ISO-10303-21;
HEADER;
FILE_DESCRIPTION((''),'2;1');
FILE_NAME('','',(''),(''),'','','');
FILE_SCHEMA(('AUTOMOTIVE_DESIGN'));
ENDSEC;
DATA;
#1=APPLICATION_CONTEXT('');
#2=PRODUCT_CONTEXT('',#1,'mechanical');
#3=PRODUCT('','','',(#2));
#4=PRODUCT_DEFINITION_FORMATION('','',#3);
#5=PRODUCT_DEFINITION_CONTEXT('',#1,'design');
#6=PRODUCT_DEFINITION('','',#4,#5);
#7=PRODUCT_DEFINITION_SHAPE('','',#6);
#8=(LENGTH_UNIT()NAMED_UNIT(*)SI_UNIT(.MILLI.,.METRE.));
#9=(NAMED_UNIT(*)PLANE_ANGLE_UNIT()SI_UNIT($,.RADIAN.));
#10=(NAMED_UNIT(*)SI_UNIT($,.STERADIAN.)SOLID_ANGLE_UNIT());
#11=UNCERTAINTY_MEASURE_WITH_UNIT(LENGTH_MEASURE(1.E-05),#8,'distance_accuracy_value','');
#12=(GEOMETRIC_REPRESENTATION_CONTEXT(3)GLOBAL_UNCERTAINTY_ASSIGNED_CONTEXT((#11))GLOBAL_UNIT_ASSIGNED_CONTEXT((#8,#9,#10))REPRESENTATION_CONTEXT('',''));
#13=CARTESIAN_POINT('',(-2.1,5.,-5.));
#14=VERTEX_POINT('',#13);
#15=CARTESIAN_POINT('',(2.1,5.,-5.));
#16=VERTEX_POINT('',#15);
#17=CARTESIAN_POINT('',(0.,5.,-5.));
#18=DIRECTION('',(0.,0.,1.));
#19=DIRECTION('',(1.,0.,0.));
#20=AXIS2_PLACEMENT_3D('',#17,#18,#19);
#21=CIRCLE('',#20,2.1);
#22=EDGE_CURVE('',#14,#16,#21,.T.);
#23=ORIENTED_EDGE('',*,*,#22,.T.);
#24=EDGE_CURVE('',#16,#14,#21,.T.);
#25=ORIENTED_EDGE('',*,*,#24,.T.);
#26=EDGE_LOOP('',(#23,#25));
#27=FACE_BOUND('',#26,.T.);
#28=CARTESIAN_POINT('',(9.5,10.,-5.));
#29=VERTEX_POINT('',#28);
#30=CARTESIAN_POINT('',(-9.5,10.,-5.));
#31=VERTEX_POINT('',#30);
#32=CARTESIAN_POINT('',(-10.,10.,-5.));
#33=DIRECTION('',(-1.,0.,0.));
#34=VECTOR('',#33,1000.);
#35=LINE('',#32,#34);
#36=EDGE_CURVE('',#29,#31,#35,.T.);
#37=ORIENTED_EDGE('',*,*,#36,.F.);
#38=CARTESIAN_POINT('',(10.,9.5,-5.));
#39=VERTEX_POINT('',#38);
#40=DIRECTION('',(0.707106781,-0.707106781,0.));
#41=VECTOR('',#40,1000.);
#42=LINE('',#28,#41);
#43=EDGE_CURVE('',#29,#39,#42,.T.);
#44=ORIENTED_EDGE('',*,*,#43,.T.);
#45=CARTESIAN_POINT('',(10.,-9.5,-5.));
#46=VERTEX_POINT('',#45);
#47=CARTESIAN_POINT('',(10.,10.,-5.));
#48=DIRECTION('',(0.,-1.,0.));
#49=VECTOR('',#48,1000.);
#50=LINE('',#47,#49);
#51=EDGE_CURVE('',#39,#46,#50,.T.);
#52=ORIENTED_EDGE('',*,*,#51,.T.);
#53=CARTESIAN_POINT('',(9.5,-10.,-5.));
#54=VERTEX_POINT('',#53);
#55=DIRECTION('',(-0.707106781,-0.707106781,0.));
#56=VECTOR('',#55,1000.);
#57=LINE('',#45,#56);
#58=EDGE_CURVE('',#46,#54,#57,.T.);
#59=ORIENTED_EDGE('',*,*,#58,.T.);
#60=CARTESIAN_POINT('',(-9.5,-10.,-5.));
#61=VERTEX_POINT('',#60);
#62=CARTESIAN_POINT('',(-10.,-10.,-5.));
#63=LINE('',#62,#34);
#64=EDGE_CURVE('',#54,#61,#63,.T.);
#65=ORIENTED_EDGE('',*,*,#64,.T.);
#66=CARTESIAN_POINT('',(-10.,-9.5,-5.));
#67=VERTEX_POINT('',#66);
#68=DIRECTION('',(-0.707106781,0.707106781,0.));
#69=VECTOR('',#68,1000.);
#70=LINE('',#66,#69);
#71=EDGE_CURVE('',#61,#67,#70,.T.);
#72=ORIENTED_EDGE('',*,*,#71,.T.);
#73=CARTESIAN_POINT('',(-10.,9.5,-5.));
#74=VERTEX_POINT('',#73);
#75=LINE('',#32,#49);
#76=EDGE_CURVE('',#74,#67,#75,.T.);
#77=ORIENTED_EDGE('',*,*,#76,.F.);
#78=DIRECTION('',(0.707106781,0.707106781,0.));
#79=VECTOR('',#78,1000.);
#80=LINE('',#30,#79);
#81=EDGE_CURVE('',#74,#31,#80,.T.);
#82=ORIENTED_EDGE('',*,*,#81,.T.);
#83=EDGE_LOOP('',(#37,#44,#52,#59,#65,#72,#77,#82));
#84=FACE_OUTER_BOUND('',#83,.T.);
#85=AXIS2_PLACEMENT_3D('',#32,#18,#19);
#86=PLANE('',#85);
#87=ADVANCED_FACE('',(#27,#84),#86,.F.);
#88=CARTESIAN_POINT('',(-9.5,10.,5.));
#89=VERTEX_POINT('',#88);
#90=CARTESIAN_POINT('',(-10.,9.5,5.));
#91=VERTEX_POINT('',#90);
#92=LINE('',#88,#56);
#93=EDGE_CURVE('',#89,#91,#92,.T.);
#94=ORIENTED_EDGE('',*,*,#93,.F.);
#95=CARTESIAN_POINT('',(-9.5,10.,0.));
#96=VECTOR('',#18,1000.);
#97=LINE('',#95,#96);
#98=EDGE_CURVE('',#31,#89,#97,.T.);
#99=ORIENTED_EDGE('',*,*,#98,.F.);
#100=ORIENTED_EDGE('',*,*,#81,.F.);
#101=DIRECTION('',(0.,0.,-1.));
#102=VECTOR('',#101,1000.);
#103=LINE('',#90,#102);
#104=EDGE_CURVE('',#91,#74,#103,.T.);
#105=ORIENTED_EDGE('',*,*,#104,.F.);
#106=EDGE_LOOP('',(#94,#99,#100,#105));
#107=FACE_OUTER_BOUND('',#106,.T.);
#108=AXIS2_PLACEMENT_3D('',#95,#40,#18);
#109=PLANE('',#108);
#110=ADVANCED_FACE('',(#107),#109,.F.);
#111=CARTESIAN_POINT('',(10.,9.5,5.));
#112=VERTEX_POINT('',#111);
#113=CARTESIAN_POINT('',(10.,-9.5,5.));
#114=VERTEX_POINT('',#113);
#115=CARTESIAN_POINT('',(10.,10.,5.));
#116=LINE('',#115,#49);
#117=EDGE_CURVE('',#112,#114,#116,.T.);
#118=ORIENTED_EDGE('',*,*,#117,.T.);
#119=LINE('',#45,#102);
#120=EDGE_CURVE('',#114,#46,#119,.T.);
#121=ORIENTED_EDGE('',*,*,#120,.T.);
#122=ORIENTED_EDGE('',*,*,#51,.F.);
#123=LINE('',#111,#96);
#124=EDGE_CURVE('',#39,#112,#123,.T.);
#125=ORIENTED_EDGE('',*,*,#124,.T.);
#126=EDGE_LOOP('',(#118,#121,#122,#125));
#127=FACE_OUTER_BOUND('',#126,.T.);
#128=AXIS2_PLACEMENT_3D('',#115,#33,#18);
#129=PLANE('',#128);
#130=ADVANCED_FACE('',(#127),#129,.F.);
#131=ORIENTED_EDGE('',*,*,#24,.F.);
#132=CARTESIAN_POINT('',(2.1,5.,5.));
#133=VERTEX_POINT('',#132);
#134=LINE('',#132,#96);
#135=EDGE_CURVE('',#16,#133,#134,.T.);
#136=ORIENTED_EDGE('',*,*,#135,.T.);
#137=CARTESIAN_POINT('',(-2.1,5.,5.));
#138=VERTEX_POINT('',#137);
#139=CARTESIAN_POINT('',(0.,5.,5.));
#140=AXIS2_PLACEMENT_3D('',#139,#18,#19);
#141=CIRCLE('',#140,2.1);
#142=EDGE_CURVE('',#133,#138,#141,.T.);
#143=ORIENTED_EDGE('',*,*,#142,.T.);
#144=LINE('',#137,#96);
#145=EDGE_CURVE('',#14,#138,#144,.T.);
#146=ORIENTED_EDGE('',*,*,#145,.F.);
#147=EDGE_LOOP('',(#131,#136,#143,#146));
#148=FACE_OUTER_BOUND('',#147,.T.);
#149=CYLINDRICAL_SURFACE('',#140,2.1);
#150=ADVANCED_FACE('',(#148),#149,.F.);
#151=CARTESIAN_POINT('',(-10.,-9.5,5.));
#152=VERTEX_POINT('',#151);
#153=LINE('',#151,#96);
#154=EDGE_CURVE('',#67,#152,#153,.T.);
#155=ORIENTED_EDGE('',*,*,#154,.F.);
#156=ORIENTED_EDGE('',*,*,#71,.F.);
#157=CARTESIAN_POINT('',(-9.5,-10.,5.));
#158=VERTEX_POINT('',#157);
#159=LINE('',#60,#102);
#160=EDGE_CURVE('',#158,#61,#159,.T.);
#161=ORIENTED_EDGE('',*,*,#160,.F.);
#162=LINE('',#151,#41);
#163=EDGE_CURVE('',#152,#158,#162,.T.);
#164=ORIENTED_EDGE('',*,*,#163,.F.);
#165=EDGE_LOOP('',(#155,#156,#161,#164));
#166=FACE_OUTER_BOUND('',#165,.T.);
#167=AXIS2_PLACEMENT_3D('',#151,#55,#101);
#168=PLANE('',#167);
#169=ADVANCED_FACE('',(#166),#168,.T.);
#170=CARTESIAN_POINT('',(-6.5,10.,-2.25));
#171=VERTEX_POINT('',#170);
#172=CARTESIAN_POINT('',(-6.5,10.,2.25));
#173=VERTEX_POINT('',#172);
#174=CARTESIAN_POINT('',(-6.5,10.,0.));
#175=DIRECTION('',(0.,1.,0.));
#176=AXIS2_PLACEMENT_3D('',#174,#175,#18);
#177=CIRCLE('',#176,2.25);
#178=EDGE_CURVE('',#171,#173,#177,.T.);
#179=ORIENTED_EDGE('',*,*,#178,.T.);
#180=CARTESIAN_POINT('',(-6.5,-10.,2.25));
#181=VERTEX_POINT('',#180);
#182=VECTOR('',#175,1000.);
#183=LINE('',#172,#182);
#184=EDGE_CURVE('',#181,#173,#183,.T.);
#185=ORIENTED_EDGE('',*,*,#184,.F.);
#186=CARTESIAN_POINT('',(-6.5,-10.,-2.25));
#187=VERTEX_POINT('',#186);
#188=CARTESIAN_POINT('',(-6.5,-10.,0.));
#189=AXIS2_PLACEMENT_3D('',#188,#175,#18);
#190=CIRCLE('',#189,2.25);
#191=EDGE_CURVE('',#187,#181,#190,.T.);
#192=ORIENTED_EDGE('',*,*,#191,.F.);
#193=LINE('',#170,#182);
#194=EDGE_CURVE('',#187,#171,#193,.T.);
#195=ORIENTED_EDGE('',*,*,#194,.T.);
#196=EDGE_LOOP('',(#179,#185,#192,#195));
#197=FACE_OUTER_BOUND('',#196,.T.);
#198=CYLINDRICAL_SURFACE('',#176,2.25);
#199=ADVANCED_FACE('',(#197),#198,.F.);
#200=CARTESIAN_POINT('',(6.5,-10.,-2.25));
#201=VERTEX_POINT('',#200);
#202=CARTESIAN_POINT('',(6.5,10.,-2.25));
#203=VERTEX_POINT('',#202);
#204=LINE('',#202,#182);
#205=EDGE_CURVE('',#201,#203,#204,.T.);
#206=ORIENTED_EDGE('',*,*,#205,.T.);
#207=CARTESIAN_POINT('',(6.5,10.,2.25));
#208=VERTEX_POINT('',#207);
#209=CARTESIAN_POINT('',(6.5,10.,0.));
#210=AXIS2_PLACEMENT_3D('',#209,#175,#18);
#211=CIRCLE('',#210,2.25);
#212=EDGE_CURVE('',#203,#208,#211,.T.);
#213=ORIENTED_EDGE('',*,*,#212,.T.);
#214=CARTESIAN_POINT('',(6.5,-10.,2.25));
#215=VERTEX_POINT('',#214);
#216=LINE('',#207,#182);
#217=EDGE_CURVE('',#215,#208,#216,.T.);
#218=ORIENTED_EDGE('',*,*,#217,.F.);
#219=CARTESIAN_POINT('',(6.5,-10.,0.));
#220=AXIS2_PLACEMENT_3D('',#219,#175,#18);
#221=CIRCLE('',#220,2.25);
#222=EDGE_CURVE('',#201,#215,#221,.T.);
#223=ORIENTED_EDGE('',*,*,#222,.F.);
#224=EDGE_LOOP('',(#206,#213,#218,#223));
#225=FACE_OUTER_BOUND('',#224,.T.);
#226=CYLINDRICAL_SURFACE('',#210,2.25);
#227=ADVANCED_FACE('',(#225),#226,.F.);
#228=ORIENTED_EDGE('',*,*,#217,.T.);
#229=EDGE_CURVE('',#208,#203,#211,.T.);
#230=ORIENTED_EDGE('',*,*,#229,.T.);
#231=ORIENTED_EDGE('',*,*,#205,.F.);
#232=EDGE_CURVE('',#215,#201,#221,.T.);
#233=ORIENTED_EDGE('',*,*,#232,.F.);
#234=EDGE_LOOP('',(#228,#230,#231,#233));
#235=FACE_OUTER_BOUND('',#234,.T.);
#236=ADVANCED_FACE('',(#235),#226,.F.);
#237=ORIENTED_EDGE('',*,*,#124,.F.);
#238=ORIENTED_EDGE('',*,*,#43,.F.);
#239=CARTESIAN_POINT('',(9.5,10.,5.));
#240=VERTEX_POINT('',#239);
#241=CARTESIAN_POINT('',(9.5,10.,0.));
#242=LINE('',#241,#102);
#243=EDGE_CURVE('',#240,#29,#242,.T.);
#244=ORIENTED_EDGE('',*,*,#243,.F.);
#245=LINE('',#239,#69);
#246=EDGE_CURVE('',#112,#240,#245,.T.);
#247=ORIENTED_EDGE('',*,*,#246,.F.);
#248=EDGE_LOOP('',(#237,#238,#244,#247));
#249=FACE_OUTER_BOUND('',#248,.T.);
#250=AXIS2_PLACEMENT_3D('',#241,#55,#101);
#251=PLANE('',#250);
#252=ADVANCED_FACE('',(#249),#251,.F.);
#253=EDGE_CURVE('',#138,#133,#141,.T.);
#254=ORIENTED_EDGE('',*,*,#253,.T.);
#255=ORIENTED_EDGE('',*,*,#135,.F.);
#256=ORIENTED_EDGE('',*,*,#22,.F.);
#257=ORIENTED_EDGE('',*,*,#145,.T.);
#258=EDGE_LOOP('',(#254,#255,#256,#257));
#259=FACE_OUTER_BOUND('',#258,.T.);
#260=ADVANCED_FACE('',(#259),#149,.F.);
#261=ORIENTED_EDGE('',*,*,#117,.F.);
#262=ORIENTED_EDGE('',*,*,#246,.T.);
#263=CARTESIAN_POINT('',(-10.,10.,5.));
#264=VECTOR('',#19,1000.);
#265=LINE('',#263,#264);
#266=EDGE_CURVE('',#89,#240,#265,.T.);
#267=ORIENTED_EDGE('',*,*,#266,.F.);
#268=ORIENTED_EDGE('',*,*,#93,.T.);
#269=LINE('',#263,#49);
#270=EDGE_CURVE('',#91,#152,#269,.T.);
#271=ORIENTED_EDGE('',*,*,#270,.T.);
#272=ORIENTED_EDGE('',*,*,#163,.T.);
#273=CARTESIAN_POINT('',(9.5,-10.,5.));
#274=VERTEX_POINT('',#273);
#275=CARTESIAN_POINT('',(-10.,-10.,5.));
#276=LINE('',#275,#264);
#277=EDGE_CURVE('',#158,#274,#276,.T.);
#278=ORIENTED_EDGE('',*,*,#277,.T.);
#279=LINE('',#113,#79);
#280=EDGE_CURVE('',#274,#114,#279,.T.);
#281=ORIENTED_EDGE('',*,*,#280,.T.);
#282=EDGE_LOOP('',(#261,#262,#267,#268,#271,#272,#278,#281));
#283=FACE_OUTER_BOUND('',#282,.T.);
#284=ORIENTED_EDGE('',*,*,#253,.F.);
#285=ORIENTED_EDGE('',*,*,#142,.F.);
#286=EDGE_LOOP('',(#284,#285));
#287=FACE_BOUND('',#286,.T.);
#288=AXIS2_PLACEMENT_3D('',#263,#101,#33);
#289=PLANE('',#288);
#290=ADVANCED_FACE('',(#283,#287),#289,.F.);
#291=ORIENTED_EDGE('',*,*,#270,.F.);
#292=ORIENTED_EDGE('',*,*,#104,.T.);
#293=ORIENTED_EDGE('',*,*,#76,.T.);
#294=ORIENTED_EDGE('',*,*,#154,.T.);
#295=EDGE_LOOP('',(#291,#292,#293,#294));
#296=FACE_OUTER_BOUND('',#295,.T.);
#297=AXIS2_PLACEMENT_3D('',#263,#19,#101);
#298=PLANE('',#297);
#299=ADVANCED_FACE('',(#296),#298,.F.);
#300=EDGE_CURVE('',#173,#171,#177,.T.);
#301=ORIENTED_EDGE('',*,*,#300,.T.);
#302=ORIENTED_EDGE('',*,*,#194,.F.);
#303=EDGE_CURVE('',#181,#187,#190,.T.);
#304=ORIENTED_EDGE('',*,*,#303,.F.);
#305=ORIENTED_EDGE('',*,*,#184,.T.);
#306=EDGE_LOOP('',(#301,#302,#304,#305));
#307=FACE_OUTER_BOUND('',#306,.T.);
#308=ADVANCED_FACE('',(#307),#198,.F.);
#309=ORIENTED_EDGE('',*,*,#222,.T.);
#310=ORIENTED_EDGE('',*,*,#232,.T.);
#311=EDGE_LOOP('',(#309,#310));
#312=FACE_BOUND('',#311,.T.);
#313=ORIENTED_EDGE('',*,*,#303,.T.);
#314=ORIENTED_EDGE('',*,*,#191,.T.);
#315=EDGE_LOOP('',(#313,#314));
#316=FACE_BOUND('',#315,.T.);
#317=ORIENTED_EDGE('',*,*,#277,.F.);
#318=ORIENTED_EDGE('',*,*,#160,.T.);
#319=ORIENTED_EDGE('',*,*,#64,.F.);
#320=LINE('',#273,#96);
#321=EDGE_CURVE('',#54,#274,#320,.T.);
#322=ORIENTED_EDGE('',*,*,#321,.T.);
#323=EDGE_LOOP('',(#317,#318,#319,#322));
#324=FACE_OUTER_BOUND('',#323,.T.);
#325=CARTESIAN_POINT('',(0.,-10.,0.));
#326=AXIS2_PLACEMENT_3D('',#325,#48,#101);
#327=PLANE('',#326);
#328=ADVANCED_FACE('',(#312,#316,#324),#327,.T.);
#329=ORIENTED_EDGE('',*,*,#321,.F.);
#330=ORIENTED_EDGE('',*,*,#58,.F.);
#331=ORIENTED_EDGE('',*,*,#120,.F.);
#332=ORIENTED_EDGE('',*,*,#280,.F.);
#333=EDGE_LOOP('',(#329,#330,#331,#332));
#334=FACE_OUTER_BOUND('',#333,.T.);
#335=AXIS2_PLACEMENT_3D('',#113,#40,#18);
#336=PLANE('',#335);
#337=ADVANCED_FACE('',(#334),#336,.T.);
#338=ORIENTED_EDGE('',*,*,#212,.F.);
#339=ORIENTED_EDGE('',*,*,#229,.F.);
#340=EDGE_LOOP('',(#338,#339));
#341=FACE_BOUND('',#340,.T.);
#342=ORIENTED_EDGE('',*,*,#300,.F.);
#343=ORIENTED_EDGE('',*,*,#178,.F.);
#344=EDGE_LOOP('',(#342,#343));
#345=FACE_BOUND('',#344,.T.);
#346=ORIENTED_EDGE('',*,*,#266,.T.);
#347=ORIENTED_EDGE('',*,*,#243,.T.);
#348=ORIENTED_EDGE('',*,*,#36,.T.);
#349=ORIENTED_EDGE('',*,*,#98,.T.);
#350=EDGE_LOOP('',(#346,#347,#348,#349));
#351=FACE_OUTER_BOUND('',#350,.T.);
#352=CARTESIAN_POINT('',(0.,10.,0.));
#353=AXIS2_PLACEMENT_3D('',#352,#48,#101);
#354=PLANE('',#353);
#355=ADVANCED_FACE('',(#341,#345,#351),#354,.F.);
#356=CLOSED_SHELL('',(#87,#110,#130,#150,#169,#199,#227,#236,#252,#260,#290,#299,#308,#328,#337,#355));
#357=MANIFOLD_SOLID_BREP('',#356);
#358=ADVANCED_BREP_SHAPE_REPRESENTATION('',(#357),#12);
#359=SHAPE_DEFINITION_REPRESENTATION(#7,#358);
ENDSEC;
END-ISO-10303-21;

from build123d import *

# Parameters (mm, degrees)
SKETCH1_W            = 20
SKETCH1_H            = 10
BOSS_EXTRUDE1_DEPTH  = 10
M5_TAPPED_HOLE1_D    = 4.2
M4_CLEARANCE_HOLE1_D = 4.5
CHAMFER1_SIZE        = 0.5


with BuildPart() as part:
    # Sketch1 → Boss-Extrude1 (new, symmetric)
    with BuildSketch(Plane(origin=(0, 0, 0), x_dir=(1, 0, 0), z_dir=(0, 1, 0))):
        Rectangle(SKETCH1_W, SKETCH1_H)
    extrude(amount=BOSS_EXTRUDE1_DEPTH, both=True)

    # M5 Tapped Hole1 (through all)
    with Locations(Plane.XY.offset(5)):
        with Locations((0, 5)):
            Hole(M5_TAPPED_HOLE1_D / 2)

    # M4 Clearance Hole1 (through all)
    with Locations(Plane(origin=(0, 10, 0), x_dir=(1, 0, 0), z_dir=(0, 1, 0))):
        with Locations((6.5, 0), (-6.5, 0)):
            Hole(M4_CLEARANCE_HOLE1_D / 2)

    # Chamfer1
    chamfer1_edges = [part.edges().sort_by_distance(p)[0] for p in [
        (-10, 10, 0),
        (10, 10, 0),
        (-10, -10, 0),
        (10, -10, 0),
    ]]
    chamfer(chamfer1_edges, length=CHAMFER1_SIZE)


solid = part.part
